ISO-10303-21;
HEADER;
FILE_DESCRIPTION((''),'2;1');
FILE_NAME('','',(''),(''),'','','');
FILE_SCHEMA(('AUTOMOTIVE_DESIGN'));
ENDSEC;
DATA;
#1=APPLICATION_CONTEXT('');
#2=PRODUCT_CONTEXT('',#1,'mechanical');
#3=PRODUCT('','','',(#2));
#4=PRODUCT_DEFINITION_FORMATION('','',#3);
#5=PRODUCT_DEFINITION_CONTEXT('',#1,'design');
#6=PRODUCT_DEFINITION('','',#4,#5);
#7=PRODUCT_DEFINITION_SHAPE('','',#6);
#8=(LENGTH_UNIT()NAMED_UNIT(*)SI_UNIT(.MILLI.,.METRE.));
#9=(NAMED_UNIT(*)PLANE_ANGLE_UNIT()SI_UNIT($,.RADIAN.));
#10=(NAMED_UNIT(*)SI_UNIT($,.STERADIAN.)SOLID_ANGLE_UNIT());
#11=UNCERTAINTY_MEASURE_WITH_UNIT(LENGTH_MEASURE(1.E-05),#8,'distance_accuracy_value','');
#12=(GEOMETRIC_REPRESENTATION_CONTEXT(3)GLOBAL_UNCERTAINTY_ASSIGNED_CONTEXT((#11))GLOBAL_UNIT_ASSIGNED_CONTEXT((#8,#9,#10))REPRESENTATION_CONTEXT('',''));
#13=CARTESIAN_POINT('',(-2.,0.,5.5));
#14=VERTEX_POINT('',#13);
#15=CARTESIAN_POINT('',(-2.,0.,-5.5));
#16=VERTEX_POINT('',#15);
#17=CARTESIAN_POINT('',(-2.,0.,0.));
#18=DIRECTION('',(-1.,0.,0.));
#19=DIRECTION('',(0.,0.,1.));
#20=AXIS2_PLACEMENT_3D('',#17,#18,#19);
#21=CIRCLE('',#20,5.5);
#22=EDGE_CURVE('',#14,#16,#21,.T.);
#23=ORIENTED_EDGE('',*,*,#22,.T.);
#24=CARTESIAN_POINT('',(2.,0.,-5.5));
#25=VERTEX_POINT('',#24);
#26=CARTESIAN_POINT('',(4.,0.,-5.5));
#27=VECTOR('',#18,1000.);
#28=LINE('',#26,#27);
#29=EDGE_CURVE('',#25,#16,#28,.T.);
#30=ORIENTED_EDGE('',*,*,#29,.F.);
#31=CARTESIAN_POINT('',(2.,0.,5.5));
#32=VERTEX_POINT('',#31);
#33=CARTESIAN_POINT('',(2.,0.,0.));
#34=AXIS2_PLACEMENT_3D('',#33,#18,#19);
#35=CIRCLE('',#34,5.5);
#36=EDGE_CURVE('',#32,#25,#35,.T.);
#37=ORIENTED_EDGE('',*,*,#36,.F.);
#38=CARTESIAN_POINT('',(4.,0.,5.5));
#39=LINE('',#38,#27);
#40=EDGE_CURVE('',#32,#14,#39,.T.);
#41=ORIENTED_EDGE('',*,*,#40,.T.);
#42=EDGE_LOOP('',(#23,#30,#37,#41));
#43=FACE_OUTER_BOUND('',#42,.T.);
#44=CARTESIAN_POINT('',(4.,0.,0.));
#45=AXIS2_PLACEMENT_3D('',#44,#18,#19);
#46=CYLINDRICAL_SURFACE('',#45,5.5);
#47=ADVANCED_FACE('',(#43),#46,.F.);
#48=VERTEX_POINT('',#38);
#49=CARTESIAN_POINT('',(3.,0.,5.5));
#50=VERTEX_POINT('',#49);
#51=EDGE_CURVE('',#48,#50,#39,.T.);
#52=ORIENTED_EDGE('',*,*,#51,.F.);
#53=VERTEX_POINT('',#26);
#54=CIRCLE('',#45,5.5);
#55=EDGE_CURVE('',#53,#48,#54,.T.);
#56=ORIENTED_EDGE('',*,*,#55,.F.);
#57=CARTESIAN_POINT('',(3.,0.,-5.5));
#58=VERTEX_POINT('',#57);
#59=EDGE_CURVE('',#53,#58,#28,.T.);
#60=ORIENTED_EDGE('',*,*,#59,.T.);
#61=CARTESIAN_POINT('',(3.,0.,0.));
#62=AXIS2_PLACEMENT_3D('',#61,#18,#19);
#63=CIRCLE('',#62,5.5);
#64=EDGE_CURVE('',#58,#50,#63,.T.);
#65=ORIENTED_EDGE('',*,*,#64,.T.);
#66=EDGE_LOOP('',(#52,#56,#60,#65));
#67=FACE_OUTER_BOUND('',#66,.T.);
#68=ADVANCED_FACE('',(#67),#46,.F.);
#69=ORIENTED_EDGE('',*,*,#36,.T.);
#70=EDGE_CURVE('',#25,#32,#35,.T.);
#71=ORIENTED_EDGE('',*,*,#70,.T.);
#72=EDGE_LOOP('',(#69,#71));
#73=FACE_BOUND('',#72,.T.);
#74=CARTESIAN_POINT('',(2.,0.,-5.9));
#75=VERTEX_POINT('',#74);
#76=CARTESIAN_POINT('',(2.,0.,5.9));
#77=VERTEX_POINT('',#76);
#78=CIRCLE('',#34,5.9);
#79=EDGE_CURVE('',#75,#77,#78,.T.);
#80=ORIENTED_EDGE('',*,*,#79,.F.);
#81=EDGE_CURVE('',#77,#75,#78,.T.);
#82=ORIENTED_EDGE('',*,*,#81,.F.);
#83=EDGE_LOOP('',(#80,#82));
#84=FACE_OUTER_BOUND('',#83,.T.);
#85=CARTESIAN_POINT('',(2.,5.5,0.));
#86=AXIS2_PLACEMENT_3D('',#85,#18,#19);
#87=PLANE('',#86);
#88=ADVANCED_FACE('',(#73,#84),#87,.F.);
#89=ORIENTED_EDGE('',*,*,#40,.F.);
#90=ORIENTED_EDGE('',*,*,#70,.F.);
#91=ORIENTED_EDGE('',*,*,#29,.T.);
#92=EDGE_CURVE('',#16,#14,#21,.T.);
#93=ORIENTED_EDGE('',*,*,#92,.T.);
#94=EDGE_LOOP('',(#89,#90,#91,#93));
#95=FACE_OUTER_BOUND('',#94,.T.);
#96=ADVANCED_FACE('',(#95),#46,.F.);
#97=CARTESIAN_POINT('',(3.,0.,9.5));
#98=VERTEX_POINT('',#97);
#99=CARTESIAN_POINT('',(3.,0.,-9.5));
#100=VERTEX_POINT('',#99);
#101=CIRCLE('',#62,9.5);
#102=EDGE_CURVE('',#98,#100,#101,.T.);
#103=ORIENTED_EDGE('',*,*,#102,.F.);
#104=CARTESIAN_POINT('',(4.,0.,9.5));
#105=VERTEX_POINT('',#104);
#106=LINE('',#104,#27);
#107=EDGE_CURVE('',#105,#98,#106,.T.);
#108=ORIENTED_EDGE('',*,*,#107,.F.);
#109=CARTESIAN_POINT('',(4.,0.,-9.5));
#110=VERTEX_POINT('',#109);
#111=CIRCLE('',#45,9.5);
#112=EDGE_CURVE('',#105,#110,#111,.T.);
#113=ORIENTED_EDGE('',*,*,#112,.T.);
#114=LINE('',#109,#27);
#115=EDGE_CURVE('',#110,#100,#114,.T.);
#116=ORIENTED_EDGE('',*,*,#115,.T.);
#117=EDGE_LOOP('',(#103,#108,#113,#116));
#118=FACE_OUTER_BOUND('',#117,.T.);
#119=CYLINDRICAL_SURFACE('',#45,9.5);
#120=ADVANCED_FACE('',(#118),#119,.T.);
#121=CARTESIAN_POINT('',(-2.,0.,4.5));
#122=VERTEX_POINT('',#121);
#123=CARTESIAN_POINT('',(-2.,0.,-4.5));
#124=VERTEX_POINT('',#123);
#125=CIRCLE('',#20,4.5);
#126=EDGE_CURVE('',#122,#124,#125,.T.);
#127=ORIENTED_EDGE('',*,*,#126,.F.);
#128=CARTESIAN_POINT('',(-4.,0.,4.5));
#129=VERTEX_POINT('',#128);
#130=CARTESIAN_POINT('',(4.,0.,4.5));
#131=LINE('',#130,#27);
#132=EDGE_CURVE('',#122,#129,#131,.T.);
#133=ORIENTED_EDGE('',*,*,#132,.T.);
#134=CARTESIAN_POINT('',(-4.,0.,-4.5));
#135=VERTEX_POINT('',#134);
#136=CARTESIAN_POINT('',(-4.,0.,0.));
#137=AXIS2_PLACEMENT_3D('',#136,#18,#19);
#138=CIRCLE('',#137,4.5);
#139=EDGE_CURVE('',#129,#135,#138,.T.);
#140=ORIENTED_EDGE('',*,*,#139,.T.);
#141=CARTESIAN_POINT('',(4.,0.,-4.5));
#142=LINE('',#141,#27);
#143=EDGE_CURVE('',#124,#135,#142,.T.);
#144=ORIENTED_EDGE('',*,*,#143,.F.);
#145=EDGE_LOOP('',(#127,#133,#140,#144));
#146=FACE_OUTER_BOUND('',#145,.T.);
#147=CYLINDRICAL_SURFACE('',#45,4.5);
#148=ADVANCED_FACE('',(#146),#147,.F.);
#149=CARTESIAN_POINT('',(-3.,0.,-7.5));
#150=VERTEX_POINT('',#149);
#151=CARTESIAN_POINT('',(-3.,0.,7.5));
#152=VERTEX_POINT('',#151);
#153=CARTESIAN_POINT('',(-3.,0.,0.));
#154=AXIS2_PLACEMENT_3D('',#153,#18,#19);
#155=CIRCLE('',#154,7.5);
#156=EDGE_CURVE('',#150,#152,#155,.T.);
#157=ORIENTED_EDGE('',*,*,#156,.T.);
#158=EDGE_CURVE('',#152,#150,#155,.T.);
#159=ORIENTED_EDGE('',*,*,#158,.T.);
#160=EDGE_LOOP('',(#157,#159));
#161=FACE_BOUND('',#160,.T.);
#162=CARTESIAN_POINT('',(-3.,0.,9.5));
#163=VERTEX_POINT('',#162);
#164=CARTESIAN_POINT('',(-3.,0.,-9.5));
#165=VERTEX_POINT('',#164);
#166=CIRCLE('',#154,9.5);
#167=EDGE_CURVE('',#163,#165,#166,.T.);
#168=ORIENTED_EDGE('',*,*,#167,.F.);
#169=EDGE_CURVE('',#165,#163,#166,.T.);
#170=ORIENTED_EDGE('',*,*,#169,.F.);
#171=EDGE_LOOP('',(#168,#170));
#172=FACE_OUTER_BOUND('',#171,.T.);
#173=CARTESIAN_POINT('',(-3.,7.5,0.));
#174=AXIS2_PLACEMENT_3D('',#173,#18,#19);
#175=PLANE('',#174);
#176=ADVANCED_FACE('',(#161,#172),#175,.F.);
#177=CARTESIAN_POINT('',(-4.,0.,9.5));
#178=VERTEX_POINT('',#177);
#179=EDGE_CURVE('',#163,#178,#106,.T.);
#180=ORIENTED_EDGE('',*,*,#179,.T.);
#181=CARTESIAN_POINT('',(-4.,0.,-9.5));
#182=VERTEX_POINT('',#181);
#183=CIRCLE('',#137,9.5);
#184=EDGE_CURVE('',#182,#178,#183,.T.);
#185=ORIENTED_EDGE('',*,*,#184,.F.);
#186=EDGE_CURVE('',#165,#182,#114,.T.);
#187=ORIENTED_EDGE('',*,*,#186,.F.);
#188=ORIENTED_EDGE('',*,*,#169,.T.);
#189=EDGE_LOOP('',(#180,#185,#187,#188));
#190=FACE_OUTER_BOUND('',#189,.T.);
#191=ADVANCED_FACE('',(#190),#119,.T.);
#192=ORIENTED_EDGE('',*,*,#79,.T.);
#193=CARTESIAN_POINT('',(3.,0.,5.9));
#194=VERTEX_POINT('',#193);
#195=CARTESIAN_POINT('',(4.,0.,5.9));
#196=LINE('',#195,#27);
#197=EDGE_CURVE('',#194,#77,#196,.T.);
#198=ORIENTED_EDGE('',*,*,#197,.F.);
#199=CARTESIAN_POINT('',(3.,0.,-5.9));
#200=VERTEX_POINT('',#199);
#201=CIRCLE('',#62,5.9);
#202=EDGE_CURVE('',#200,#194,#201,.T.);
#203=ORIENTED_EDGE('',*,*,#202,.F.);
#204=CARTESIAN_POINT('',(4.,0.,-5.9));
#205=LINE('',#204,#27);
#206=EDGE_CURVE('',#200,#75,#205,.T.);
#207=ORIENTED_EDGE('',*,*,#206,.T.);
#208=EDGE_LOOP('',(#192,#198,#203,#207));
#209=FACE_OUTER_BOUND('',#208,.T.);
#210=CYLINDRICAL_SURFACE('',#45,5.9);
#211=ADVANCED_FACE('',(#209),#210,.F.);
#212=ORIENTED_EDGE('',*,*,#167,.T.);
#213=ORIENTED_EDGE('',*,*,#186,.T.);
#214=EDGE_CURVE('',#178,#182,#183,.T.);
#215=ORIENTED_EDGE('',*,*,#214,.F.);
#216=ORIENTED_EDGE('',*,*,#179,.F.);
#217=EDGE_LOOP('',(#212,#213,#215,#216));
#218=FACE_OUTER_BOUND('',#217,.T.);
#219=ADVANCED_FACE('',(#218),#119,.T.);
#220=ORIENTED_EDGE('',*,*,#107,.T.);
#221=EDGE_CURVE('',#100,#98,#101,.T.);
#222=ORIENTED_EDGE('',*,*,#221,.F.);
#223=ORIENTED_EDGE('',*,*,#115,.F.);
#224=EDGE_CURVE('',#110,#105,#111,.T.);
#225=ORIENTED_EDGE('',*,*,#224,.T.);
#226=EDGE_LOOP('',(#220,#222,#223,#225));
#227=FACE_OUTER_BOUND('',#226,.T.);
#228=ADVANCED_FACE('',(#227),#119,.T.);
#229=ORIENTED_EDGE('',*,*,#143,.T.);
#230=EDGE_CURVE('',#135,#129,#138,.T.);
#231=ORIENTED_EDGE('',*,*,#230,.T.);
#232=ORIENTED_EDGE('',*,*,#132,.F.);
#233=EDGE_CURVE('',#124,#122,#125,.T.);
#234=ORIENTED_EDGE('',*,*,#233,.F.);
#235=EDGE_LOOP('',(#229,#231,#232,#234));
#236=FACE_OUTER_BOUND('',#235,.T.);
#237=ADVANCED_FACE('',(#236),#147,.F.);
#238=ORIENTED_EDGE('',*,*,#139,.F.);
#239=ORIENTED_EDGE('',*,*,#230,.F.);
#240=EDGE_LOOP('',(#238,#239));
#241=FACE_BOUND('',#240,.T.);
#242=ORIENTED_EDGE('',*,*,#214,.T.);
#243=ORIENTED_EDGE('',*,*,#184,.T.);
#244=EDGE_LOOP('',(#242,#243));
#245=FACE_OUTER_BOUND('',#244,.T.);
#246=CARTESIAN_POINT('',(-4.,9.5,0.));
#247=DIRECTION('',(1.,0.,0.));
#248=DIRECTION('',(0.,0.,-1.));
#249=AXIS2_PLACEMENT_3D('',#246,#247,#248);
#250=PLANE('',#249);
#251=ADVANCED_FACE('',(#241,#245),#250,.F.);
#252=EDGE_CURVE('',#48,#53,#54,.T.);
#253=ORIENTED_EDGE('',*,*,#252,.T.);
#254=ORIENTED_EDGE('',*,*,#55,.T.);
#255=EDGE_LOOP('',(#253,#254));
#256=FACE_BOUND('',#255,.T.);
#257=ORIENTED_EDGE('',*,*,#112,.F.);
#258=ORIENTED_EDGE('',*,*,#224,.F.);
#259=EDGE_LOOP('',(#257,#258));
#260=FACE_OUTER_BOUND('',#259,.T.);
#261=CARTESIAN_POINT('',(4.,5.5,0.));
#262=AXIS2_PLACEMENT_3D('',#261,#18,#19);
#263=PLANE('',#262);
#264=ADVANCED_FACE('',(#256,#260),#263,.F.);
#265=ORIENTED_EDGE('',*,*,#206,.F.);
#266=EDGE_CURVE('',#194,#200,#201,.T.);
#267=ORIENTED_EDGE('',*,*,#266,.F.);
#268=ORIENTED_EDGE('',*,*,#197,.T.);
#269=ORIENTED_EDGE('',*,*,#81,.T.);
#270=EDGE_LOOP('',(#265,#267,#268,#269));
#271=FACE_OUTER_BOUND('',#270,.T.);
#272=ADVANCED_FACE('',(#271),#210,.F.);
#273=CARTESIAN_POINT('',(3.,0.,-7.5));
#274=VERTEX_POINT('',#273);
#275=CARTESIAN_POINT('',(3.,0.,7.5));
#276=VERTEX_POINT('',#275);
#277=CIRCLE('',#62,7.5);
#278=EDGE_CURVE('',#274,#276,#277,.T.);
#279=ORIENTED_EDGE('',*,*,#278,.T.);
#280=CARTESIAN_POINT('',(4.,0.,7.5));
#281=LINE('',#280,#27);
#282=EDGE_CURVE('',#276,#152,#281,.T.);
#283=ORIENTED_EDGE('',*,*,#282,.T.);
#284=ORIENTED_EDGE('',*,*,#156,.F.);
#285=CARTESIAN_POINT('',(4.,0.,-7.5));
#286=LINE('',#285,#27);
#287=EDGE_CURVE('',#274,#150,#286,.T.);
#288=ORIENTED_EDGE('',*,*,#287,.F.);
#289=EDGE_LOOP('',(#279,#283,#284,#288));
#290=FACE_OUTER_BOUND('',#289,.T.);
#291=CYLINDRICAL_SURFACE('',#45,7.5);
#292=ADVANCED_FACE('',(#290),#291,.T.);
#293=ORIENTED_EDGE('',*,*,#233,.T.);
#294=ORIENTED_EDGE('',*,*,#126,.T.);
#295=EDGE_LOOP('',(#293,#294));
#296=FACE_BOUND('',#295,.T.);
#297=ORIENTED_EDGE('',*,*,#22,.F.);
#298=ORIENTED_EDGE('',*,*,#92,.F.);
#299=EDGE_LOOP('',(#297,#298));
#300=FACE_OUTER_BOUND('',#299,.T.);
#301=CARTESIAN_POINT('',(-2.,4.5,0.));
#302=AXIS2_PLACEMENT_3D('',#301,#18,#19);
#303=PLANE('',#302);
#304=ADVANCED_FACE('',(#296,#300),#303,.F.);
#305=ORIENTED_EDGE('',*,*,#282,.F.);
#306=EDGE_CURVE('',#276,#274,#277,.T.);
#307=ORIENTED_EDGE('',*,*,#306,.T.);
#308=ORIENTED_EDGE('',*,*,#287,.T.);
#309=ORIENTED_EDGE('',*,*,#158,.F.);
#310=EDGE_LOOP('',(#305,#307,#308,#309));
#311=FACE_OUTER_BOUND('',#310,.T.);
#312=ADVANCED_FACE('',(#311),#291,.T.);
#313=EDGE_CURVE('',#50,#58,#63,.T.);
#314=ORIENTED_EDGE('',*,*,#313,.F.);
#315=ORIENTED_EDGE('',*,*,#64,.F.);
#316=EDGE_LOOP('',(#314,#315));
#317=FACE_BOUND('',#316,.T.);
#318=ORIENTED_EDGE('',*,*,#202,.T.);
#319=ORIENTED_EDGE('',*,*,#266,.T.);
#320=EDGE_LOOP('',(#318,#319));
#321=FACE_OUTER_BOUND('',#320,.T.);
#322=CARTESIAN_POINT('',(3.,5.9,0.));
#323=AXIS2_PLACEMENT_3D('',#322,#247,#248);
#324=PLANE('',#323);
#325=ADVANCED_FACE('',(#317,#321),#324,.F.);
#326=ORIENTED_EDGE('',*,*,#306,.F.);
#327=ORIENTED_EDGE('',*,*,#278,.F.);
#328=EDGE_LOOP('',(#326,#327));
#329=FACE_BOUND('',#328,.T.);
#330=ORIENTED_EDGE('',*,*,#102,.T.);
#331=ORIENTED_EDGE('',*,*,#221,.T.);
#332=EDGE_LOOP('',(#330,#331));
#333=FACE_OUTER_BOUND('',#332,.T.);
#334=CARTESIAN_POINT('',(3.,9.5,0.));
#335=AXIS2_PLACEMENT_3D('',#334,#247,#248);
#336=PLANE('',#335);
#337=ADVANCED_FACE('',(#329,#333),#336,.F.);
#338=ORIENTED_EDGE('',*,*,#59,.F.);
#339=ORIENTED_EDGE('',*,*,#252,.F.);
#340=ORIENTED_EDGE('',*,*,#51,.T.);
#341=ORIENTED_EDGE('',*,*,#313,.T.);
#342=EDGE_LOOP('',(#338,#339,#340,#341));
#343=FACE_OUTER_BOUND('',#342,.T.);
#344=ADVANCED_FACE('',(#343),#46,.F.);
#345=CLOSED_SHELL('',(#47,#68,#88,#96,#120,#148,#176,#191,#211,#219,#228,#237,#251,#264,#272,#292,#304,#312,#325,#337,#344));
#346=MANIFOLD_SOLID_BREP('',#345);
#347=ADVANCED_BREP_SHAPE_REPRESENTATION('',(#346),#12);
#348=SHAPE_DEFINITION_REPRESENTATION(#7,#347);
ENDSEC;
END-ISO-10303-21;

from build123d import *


with BuildPart() as part:
    # 草图1 → 旋转1 (revolve)
    with BuildSketch(Plane.XY, mode=Mode.PRIVATE) as revolve_1_sk:
        Polygon((-4, 4.5), (-2, 4.5), (-2, 5.5), (2, 5.5), (2, 5.9), (3, 5.9), (3, 5.5), (4, 5.5), (4, 9.5), (3, 9.5), (3, 7.5), (-3, 7.5), (-3, 9.5), (-4, 9.5), align=None)
    revolve(revolve_1_sk.sketch.rotate(Axis((4, 0, 0), (-1, 0, 0)), 270), axis=Axis((4, 0, 0), (-1, 0, 0)))


solid = part.part
